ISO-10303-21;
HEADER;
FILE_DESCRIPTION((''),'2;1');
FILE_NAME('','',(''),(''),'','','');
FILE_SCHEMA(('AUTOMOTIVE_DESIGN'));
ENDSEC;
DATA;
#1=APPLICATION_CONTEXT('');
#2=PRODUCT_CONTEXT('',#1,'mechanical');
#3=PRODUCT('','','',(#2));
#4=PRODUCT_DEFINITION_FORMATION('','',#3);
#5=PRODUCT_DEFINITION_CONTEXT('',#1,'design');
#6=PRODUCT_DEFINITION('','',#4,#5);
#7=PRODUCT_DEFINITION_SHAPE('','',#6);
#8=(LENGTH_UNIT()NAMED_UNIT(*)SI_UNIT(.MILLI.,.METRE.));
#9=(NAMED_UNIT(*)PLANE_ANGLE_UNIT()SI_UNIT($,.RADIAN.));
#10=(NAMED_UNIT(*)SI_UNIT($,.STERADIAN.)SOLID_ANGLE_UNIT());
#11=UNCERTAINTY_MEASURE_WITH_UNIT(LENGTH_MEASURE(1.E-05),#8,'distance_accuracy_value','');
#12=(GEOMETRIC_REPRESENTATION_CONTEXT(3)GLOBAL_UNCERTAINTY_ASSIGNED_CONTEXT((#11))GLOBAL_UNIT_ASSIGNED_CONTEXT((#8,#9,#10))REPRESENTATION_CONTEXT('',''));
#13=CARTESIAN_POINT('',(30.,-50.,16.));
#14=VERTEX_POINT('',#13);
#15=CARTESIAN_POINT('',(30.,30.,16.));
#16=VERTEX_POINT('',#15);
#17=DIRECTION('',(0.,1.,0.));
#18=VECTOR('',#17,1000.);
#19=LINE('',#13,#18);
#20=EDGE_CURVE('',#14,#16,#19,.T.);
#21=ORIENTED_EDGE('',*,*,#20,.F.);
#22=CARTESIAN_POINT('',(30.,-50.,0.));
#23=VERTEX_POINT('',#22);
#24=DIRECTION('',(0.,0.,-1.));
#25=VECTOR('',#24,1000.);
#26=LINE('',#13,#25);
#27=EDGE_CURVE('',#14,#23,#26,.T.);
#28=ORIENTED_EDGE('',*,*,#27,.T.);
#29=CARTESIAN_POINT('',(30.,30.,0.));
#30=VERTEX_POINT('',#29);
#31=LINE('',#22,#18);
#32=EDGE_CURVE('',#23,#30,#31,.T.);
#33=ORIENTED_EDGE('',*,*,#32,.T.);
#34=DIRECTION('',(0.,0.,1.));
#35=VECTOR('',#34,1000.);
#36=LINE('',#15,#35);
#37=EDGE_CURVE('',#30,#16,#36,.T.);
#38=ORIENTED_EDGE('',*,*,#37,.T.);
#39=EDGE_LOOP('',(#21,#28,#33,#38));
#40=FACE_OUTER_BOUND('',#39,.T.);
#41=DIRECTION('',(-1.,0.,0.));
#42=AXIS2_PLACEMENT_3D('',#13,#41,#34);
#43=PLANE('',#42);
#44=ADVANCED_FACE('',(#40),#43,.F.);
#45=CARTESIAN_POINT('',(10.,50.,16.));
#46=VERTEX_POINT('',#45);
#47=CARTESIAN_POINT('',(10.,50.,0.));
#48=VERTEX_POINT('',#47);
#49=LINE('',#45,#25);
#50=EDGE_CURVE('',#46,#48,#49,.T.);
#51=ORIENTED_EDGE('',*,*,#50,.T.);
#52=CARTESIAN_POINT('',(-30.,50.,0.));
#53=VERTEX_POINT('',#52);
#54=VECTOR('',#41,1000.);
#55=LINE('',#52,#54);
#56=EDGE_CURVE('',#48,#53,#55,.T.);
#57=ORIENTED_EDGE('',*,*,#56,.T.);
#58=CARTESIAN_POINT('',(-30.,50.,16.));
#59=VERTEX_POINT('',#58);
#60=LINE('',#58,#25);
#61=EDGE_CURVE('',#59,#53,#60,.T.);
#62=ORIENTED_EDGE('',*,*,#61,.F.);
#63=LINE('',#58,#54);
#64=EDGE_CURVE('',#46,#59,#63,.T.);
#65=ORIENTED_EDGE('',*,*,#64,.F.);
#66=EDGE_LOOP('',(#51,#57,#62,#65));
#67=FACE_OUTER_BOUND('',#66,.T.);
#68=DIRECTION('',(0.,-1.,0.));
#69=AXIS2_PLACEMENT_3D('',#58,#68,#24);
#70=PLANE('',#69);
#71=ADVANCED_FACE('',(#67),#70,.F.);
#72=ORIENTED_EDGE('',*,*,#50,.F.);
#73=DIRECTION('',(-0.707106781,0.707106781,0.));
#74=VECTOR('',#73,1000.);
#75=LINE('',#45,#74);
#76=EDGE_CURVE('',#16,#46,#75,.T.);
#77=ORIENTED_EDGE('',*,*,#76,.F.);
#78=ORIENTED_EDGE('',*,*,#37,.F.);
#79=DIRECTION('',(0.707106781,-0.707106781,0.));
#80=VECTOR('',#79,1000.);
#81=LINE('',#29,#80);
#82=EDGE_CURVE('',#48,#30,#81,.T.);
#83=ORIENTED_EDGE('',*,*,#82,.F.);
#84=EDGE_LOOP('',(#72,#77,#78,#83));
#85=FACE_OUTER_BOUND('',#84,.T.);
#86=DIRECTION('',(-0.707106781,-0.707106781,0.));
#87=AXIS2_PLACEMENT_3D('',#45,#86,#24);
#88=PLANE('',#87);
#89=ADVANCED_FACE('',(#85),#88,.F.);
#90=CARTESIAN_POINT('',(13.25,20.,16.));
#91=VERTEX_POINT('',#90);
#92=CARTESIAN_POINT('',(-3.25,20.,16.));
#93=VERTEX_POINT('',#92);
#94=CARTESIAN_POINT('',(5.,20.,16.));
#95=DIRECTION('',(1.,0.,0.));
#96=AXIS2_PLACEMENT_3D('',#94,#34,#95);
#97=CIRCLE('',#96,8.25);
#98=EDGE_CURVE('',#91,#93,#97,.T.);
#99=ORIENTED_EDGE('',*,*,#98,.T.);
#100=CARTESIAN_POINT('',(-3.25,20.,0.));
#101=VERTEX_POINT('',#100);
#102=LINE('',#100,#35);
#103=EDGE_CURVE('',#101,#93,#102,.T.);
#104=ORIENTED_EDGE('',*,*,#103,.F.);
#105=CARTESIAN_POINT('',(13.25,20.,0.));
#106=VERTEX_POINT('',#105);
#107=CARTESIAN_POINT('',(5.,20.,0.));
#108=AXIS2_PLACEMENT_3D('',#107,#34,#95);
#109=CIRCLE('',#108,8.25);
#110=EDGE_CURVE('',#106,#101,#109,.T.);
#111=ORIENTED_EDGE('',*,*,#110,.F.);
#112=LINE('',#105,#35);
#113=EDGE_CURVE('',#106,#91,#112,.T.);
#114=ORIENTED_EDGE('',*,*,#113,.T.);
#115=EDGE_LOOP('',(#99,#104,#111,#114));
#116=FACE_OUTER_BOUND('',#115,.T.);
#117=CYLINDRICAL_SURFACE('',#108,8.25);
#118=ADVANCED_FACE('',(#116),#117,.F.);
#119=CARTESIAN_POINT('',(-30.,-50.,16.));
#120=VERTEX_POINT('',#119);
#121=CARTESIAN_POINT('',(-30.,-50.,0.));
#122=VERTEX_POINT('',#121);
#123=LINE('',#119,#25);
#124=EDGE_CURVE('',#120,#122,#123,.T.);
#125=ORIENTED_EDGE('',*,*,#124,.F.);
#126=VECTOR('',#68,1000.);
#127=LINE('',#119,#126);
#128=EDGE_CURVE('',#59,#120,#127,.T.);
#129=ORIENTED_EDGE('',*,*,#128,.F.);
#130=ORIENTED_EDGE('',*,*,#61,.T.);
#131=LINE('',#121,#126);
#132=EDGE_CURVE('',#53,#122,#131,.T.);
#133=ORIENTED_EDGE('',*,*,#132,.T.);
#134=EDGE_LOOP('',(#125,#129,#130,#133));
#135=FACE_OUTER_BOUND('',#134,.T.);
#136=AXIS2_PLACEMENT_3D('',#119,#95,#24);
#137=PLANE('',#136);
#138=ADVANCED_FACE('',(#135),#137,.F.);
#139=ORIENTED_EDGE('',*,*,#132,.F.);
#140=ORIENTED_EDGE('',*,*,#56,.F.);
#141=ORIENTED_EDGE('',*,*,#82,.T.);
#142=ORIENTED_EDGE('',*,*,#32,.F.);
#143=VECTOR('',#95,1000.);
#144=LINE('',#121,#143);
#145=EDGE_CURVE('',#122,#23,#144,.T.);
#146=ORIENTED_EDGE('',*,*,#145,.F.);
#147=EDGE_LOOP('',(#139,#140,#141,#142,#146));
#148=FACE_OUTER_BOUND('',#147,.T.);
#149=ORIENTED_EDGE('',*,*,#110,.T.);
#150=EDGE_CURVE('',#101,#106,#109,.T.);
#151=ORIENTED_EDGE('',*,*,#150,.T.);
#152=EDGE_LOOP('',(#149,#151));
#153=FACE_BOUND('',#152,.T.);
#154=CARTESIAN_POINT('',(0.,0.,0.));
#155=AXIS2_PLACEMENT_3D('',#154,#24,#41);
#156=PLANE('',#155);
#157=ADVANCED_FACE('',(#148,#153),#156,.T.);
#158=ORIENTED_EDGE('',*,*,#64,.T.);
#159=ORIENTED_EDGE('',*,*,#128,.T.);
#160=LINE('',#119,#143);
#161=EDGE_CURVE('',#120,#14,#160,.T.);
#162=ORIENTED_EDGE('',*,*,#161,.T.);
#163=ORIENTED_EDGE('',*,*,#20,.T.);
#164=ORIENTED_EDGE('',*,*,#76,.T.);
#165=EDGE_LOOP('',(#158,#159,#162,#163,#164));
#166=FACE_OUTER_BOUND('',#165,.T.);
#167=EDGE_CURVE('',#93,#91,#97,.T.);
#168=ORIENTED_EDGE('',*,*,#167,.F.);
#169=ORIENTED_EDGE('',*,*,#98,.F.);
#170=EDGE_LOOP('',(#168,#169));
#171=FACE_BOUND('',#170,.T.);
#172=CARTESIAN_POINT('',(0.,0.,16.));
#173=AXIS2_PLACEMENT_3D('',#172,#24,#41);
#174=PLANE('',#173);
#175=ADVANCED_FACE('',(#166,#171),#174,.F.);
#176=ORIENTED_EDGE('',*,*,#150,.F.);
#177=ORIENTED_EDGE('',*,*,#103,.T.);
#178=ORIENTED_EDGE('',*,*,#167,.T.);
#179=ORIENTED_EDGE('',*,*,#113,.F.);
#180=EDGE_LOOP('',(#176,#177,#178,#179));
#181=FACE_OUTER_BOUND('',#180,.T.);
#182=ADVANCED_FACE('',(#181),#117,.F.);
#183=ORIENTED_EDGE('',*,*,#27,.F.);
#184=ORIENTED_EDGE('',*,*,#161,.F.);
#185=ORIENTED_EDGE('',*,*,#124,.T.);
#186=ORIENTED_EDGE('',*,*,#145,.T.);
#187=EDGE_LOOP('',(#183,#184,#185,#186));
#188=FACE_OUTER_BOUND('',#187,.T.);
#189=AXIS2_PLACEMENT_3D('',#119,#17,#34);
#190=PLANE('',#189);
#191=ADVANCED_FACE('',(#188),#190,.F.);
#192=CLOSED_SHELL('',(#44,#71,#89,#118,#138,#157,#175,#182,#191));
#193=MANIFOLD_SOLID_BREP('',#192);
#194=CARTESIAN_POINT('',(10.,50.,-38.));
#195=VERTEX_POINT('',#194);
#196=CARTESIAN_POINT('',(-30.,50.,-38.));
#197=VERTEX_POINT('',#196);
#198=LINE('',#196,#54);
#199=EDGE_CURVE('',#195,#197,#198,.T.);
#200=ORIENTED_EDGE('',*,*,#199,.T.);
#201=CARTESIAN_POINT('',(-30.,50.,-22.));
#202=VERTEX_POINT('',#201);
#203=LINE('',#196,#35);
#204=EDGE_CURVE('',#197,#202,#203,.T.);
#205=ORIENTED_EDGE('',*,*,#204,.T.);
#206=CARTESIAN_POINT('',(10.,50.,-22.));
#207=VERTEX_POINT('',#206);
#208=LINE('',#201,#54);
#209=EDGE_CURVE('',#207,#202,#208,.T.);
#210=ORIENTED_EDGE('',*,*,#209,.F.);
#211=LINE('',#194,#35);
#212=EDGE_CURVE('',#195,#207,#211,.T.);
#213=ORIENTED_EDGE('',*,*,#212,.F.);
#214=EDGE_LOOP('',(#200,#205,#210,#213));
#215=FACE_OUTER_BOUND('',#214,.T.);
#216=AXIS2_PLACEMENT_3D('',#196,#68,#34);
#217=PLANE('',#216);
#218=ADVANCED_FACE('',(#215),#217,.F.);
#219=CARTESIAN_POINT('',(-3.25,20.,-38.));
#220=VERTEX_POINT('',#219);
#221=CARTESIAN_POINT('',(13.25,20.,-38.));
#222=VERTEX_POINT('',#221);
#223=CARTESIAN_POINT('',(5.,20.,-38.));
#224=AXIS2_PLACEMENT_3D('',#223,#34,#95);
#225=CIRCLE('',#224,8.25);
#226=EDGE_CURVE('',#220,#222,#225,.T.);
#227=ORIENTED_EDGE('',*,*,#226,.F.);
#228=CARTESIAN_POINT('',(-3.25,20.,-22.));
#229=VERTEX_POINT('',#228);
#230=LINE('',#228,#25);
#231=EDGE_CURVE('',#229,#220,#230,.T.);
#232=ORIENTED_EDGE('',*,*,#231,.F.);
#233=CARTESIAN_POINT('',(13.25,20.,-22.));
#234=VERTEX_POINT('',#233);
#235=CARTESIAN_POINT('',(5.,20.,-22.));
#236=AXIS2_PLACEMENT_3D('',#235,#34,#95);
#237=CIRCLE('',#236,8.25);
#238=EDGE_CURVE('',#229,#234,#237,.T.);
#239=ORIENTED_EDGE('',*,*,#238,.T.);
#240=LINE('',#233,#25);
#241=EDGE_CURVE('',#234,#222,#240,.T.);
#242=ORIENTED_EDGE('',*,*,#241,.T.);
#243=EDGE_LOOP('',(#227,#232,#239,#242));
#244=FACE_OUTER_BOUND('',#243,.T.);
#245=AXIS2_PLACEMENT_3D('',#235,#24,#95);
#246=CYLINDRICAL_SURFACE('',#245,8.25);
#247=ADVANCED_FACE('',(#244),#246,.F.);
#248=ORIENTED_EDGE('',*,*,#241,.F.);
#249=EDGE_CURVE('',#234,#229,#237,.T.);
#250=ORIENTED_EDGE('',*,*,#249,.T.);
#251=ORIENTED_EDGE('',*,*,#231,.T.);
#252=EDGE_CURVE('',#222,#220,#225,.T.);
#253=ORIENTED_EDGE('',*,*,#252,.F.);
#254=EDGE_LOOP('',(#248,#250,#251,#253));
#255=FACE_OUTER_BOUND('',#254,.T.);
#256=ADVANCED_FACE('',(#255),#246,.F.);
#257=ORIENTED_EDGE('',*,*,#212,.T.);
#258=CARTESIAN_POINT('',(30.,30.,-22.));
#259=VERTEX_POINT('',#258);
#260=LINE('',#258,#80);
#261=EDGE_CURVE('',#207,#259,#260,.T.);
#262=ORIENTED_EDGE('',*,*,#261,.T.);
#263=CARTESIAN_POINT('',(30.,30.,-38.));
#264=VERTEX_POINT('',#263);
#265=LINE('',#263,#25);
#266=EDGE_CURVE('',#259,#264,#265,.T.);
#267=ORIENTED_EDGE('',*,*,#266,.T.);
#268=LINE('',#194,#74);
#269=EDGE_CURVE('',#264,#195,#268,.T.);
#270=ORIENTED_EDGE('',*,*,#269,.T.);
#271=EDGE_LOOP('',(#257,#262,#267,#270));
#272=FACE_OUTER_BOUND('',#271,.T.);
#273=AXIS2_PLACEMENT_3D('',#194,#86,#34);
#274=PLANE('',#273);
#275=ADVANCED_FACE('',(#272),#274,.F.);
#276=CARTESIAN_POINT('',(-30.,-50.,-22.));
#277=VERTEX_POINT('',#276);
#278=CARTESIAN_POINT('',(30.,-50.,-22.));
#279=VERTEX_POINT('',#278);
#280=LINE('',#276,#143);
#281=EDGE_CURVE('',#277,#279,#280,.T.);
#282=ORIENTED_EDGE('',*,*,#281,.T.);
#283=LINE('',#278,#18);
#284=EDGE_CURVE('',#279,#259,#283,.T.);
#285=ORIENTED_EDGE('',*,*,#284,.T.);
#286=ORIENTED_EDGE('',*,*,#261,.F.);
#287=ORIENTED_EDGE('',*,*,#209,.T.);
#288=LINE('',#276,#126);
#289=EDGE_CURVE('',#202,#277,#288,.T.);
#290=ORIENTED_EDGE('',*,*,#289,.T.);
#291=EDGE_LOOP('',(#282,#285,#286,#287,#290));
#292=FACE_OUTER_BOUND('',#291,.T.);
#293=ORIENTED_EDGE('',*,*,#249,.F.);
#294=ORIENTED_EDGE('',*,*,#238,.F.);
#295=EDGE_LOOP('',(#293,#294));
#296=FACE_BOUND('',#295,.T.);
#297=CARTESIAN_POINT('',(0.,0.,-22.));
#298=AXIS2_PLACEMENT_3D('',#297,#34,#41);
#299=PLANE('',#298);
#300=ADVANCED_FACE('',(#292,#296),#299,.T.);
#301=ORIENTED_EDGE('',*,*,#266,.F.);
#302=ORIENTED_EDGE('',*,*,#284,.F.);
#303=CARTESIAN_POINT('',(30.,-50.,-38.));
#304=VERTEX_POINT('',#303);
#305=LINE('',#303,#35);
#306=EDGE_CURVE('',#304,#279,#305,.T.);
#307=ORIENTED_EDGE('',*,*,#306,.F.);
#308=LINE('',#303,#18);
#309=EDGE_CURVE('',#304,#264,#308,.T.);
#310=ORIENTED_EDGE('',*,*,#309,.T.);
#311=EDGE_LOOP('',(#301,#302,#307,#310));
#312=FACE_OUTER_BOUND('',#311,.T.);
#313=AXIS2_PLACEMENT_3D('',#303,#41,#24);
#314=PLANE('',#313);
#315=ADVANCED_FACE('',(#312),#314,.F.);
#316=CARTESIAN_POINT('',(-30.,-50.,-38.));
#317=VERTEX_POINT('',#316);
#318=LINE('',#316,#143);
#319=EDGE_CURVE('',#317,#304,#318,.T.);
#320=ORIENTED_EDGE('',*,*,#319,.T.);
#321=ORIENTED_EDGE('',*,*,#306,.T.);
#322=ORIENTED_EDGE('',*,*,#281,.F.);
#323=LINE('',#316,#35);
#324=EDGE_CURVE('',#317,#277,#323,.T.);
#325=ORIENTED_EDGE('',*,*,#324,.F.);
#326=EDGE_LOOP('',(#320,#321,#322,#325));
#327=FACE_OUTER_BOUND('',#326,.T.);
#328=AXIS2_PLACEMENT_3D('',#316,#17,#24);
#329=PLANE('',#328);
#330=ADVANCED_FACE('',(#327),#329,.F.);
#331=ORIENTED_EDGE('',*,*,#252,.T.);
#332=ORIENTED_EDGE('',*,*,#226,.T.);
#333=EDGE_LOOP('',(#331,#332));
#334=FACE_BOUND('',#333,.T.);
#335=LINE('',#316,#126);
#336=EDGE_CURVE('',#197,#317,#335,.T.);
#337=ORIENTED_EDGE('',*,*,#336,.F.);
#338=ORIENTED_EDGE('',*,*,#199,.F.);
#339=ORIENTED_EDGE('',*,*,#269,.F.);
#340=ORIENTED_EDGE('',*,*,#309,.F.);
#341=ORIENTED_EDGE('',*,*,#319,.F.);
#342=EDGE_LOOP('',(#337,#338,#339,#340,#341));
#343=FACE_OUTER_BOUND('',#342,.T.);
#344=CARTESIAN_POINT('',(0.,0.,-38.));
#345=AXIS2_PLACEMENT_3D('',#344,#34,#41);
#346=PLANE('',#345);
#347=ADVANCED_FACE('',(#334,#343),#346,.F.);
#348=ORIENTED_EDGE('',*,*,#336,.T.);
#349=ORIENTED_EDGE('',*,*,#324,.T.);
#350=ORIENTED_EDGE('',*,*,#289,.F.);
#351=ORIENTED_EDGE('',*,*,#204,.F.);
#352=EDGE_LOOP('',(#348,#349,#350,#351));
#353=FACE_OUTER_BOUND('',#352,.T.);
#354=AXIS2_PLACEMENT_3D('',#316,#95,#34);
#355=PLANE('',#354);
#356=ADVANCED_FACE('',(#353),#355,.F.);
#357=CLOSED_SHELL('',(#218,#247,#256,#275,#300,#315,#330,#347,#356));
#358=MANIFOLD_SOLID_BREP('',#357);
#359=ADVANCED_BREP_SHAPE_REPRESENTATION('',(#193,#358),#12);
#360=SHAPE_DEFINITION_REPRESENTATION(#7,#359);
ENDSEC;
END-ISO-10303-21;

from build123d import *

# Parameters (mm, degrees)
SKETCH1_W           = 60
SKETCH1_H           = 100
BOSS_EXTRUDE1_DEPTH = 16
SKETCH2_R           = 8.25
CUT_EXTRUDE1_DEPTH  = 16
CHAMFER1_SIZE       = 20


with BuildPart() as part:
    # Sketch1 → Boss-Extrude1 (new body)
    with BuildSketch(Plane.XY):
        Rectangle(SKETCH1_W, SKETCH1_H)
    extrude(amount=BOSS_EXTRUDE1_DEPTH)

    # Sketch2 → Cut-Extrude1 (cut)
    with BuildSketch(Plane.XY.offset(16)):
        with Locations((5, 20)):
            Circle(SKETCH2_R)
    extrude(amount=-CUT_EXTRUDE1_DEPTH, mode=Mode.SUBTRACT)

    # Chamfer1
    chamfer1_edges = [part.edges().sort_by_distance(p)[0] for p in [
        (30, 50, 8),
    ]]
    chamfer(chamfer1_edges, length=CHAMFER1_SIZE)


with BuildPart() as body_2:
    # Mirror1: mirrored copy
    add(part.part.mirror(Plane(origin=(0, 0, -11), x_dir=(1, 0, 0), z_dir=(0, 0, -1))))


solid = Compound([part.part, body_2.part])
